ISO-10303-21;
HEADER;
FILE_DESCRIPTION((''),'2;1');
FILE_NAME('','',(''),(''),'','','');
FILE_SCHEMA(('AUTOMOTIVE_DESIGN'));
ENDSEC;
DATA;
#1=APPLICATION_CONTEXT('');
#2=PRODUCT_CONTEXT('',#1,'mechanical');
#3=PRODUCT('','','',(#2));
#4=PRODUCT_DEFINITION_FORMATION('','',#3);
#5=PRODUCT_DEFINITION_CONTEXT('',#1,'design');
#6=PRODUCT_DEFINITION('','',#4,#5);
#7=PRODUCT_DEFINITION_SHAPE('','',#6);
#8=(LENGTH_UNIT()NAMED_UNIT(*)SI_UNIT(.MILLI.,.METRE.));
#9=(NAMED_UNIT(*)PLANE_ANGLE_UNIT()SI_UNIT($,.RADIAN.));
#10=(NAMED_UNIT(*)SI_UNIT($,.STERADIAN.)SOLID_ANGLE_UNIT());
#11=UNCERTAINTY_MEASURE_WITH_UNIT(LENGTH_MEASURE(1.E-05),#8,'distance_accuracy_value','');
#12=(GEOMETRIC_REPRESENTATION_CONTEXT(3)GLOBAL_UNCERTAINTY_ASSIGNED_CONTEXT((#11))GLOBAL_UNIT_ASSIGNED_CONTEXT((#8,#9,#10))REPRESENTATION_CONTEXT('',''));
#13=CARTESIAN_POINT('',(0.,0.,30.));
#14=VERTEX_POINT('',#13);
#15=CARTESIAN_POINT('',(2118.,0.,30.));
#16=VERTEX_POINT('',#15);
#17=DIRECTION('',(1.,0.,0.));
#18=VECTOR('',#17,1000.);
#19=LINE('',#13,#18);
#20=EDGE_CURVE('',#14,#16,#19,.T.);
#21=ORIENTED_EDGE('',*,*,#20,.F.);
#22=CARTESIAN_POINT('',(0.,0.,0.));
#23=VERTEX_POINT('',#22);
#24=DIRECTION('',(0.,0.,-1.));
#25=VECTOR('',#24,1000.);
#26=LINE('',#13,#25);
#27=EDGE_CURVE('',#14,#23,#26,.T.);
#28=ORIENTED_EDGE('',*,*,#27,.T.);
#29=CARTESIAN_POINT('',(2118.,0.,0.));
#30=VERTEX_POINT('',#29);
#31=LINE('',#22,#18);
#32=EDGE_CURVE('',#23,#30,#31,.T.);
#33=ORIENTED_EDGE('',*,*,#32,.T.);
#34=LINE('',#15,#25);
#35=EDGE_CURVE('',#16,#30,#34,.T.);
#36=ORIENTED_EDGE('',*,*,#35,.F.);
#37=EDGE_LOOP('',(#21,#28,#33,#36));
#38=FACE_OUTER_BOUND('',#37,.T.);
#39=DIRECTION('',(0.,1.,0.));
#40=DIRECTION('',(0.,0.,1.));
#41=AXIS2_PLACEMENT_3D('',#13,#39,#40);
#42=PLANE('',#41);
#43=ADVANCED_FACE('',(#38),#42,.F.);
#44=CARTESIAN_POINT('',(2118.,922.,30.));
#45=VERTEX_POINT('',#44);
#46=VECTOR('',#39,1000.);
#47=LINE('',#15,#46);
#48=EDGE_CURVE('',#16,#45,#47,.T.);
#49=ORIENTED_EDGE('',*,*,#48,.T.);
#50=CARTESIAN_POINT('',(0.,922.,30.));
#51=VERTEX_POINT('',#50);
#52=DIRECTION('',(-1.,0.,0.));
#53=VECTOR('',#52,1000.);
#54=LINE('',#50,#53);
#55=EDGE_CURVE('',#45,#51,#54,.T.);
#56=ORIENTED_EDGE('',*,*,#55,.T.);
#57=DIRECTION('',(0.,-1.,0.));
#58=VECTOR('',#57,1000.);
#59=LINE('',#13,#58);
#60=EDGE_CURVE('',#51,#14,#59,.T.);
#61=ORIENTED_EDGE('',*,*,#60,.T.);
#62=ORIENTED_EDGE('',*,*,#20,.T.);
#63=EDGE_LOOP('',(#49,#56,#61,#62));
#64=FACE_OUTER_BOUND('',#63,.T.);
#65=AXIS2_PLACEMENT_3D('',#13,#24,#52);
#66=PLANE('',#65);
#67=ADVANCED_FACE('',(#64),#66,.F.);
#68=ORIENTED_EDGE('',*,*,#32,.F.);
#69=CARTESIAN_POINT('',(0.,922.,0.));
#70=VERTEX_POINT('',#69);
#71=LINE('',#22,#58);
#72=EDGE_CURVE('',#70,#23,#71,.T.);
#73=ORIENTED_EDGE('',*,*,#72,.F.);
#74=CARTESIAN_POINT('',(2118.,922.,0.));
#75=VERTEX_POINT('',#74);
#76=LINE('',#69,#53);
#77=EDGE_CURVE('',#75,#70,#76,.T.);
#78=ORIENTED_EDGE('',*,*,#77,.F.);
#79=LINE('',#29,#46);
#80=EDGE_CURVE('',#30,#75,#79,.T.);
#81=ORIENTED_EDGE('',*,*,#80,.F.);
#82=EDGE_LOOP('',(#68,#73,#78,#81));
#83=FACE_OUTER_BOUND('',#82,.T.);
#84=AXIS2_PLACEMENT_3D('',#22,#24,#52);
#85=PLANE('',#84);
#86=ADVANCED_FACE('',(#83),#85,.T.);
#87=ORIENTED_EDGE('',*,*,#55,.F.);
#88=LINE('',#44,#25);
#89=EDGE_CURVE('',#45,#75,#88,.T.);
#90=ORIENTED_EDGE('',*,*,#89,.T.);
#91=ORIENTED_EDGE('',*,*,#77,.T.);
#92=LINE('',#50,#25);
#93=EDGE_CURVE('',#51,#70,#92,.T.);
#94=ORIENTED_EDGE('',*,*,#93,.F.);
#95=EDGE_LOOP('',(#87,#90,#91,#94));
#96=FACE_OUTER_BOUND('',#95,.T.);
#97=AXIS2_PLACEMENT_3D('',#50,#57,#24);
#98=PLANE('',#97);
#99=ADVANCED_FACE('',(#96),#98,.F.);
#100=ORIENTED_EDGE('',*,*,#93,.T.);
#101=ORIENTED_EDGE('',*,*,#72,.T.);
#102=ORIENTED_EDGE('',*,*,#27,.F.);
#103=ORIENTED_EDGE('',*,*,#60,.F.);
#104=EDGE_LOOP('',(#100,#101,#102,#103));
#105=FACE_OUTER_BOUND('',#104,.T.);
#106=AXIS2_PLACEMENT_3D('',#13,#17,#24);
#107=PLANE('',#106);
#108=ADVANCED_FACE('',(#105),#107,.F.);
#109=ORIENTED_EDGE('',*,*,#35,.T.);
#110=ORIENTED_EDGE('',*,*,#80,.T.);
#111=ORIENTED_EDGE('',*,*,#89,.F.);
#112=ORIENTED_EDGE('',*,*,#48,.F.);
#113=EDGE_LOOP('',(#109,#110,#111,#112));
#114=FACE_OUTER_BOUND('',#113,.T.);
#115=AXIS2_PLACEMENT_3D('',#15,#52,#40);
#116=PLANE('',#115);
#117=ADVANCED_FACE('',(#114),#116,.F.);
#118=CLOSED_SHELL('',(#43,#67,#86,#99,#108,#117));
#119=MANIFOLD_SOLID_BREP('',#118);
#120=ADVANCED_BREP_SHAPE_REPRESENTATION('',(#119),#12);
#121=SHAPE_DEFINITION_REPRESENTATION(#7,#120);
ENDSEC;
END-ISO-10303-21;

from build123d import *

# Parameters (mm, degrees)
SKETCH1_W           = 2118
SKETCH1_H           = 922
BOSS_EXTRUDE1_DEPTH = 30


with BuildPart() as part:
    # Sketch1 → Boss-Extrude1 (new body)
    with BuildSketch(Plane.XY):
        with Locations((1059, 461)):
            Rectangle(SKETCH1_W, SKETCH1_H)
    extrude(amount=BOSS_EXTRUDE1_DEPTH)


solid = part.part
